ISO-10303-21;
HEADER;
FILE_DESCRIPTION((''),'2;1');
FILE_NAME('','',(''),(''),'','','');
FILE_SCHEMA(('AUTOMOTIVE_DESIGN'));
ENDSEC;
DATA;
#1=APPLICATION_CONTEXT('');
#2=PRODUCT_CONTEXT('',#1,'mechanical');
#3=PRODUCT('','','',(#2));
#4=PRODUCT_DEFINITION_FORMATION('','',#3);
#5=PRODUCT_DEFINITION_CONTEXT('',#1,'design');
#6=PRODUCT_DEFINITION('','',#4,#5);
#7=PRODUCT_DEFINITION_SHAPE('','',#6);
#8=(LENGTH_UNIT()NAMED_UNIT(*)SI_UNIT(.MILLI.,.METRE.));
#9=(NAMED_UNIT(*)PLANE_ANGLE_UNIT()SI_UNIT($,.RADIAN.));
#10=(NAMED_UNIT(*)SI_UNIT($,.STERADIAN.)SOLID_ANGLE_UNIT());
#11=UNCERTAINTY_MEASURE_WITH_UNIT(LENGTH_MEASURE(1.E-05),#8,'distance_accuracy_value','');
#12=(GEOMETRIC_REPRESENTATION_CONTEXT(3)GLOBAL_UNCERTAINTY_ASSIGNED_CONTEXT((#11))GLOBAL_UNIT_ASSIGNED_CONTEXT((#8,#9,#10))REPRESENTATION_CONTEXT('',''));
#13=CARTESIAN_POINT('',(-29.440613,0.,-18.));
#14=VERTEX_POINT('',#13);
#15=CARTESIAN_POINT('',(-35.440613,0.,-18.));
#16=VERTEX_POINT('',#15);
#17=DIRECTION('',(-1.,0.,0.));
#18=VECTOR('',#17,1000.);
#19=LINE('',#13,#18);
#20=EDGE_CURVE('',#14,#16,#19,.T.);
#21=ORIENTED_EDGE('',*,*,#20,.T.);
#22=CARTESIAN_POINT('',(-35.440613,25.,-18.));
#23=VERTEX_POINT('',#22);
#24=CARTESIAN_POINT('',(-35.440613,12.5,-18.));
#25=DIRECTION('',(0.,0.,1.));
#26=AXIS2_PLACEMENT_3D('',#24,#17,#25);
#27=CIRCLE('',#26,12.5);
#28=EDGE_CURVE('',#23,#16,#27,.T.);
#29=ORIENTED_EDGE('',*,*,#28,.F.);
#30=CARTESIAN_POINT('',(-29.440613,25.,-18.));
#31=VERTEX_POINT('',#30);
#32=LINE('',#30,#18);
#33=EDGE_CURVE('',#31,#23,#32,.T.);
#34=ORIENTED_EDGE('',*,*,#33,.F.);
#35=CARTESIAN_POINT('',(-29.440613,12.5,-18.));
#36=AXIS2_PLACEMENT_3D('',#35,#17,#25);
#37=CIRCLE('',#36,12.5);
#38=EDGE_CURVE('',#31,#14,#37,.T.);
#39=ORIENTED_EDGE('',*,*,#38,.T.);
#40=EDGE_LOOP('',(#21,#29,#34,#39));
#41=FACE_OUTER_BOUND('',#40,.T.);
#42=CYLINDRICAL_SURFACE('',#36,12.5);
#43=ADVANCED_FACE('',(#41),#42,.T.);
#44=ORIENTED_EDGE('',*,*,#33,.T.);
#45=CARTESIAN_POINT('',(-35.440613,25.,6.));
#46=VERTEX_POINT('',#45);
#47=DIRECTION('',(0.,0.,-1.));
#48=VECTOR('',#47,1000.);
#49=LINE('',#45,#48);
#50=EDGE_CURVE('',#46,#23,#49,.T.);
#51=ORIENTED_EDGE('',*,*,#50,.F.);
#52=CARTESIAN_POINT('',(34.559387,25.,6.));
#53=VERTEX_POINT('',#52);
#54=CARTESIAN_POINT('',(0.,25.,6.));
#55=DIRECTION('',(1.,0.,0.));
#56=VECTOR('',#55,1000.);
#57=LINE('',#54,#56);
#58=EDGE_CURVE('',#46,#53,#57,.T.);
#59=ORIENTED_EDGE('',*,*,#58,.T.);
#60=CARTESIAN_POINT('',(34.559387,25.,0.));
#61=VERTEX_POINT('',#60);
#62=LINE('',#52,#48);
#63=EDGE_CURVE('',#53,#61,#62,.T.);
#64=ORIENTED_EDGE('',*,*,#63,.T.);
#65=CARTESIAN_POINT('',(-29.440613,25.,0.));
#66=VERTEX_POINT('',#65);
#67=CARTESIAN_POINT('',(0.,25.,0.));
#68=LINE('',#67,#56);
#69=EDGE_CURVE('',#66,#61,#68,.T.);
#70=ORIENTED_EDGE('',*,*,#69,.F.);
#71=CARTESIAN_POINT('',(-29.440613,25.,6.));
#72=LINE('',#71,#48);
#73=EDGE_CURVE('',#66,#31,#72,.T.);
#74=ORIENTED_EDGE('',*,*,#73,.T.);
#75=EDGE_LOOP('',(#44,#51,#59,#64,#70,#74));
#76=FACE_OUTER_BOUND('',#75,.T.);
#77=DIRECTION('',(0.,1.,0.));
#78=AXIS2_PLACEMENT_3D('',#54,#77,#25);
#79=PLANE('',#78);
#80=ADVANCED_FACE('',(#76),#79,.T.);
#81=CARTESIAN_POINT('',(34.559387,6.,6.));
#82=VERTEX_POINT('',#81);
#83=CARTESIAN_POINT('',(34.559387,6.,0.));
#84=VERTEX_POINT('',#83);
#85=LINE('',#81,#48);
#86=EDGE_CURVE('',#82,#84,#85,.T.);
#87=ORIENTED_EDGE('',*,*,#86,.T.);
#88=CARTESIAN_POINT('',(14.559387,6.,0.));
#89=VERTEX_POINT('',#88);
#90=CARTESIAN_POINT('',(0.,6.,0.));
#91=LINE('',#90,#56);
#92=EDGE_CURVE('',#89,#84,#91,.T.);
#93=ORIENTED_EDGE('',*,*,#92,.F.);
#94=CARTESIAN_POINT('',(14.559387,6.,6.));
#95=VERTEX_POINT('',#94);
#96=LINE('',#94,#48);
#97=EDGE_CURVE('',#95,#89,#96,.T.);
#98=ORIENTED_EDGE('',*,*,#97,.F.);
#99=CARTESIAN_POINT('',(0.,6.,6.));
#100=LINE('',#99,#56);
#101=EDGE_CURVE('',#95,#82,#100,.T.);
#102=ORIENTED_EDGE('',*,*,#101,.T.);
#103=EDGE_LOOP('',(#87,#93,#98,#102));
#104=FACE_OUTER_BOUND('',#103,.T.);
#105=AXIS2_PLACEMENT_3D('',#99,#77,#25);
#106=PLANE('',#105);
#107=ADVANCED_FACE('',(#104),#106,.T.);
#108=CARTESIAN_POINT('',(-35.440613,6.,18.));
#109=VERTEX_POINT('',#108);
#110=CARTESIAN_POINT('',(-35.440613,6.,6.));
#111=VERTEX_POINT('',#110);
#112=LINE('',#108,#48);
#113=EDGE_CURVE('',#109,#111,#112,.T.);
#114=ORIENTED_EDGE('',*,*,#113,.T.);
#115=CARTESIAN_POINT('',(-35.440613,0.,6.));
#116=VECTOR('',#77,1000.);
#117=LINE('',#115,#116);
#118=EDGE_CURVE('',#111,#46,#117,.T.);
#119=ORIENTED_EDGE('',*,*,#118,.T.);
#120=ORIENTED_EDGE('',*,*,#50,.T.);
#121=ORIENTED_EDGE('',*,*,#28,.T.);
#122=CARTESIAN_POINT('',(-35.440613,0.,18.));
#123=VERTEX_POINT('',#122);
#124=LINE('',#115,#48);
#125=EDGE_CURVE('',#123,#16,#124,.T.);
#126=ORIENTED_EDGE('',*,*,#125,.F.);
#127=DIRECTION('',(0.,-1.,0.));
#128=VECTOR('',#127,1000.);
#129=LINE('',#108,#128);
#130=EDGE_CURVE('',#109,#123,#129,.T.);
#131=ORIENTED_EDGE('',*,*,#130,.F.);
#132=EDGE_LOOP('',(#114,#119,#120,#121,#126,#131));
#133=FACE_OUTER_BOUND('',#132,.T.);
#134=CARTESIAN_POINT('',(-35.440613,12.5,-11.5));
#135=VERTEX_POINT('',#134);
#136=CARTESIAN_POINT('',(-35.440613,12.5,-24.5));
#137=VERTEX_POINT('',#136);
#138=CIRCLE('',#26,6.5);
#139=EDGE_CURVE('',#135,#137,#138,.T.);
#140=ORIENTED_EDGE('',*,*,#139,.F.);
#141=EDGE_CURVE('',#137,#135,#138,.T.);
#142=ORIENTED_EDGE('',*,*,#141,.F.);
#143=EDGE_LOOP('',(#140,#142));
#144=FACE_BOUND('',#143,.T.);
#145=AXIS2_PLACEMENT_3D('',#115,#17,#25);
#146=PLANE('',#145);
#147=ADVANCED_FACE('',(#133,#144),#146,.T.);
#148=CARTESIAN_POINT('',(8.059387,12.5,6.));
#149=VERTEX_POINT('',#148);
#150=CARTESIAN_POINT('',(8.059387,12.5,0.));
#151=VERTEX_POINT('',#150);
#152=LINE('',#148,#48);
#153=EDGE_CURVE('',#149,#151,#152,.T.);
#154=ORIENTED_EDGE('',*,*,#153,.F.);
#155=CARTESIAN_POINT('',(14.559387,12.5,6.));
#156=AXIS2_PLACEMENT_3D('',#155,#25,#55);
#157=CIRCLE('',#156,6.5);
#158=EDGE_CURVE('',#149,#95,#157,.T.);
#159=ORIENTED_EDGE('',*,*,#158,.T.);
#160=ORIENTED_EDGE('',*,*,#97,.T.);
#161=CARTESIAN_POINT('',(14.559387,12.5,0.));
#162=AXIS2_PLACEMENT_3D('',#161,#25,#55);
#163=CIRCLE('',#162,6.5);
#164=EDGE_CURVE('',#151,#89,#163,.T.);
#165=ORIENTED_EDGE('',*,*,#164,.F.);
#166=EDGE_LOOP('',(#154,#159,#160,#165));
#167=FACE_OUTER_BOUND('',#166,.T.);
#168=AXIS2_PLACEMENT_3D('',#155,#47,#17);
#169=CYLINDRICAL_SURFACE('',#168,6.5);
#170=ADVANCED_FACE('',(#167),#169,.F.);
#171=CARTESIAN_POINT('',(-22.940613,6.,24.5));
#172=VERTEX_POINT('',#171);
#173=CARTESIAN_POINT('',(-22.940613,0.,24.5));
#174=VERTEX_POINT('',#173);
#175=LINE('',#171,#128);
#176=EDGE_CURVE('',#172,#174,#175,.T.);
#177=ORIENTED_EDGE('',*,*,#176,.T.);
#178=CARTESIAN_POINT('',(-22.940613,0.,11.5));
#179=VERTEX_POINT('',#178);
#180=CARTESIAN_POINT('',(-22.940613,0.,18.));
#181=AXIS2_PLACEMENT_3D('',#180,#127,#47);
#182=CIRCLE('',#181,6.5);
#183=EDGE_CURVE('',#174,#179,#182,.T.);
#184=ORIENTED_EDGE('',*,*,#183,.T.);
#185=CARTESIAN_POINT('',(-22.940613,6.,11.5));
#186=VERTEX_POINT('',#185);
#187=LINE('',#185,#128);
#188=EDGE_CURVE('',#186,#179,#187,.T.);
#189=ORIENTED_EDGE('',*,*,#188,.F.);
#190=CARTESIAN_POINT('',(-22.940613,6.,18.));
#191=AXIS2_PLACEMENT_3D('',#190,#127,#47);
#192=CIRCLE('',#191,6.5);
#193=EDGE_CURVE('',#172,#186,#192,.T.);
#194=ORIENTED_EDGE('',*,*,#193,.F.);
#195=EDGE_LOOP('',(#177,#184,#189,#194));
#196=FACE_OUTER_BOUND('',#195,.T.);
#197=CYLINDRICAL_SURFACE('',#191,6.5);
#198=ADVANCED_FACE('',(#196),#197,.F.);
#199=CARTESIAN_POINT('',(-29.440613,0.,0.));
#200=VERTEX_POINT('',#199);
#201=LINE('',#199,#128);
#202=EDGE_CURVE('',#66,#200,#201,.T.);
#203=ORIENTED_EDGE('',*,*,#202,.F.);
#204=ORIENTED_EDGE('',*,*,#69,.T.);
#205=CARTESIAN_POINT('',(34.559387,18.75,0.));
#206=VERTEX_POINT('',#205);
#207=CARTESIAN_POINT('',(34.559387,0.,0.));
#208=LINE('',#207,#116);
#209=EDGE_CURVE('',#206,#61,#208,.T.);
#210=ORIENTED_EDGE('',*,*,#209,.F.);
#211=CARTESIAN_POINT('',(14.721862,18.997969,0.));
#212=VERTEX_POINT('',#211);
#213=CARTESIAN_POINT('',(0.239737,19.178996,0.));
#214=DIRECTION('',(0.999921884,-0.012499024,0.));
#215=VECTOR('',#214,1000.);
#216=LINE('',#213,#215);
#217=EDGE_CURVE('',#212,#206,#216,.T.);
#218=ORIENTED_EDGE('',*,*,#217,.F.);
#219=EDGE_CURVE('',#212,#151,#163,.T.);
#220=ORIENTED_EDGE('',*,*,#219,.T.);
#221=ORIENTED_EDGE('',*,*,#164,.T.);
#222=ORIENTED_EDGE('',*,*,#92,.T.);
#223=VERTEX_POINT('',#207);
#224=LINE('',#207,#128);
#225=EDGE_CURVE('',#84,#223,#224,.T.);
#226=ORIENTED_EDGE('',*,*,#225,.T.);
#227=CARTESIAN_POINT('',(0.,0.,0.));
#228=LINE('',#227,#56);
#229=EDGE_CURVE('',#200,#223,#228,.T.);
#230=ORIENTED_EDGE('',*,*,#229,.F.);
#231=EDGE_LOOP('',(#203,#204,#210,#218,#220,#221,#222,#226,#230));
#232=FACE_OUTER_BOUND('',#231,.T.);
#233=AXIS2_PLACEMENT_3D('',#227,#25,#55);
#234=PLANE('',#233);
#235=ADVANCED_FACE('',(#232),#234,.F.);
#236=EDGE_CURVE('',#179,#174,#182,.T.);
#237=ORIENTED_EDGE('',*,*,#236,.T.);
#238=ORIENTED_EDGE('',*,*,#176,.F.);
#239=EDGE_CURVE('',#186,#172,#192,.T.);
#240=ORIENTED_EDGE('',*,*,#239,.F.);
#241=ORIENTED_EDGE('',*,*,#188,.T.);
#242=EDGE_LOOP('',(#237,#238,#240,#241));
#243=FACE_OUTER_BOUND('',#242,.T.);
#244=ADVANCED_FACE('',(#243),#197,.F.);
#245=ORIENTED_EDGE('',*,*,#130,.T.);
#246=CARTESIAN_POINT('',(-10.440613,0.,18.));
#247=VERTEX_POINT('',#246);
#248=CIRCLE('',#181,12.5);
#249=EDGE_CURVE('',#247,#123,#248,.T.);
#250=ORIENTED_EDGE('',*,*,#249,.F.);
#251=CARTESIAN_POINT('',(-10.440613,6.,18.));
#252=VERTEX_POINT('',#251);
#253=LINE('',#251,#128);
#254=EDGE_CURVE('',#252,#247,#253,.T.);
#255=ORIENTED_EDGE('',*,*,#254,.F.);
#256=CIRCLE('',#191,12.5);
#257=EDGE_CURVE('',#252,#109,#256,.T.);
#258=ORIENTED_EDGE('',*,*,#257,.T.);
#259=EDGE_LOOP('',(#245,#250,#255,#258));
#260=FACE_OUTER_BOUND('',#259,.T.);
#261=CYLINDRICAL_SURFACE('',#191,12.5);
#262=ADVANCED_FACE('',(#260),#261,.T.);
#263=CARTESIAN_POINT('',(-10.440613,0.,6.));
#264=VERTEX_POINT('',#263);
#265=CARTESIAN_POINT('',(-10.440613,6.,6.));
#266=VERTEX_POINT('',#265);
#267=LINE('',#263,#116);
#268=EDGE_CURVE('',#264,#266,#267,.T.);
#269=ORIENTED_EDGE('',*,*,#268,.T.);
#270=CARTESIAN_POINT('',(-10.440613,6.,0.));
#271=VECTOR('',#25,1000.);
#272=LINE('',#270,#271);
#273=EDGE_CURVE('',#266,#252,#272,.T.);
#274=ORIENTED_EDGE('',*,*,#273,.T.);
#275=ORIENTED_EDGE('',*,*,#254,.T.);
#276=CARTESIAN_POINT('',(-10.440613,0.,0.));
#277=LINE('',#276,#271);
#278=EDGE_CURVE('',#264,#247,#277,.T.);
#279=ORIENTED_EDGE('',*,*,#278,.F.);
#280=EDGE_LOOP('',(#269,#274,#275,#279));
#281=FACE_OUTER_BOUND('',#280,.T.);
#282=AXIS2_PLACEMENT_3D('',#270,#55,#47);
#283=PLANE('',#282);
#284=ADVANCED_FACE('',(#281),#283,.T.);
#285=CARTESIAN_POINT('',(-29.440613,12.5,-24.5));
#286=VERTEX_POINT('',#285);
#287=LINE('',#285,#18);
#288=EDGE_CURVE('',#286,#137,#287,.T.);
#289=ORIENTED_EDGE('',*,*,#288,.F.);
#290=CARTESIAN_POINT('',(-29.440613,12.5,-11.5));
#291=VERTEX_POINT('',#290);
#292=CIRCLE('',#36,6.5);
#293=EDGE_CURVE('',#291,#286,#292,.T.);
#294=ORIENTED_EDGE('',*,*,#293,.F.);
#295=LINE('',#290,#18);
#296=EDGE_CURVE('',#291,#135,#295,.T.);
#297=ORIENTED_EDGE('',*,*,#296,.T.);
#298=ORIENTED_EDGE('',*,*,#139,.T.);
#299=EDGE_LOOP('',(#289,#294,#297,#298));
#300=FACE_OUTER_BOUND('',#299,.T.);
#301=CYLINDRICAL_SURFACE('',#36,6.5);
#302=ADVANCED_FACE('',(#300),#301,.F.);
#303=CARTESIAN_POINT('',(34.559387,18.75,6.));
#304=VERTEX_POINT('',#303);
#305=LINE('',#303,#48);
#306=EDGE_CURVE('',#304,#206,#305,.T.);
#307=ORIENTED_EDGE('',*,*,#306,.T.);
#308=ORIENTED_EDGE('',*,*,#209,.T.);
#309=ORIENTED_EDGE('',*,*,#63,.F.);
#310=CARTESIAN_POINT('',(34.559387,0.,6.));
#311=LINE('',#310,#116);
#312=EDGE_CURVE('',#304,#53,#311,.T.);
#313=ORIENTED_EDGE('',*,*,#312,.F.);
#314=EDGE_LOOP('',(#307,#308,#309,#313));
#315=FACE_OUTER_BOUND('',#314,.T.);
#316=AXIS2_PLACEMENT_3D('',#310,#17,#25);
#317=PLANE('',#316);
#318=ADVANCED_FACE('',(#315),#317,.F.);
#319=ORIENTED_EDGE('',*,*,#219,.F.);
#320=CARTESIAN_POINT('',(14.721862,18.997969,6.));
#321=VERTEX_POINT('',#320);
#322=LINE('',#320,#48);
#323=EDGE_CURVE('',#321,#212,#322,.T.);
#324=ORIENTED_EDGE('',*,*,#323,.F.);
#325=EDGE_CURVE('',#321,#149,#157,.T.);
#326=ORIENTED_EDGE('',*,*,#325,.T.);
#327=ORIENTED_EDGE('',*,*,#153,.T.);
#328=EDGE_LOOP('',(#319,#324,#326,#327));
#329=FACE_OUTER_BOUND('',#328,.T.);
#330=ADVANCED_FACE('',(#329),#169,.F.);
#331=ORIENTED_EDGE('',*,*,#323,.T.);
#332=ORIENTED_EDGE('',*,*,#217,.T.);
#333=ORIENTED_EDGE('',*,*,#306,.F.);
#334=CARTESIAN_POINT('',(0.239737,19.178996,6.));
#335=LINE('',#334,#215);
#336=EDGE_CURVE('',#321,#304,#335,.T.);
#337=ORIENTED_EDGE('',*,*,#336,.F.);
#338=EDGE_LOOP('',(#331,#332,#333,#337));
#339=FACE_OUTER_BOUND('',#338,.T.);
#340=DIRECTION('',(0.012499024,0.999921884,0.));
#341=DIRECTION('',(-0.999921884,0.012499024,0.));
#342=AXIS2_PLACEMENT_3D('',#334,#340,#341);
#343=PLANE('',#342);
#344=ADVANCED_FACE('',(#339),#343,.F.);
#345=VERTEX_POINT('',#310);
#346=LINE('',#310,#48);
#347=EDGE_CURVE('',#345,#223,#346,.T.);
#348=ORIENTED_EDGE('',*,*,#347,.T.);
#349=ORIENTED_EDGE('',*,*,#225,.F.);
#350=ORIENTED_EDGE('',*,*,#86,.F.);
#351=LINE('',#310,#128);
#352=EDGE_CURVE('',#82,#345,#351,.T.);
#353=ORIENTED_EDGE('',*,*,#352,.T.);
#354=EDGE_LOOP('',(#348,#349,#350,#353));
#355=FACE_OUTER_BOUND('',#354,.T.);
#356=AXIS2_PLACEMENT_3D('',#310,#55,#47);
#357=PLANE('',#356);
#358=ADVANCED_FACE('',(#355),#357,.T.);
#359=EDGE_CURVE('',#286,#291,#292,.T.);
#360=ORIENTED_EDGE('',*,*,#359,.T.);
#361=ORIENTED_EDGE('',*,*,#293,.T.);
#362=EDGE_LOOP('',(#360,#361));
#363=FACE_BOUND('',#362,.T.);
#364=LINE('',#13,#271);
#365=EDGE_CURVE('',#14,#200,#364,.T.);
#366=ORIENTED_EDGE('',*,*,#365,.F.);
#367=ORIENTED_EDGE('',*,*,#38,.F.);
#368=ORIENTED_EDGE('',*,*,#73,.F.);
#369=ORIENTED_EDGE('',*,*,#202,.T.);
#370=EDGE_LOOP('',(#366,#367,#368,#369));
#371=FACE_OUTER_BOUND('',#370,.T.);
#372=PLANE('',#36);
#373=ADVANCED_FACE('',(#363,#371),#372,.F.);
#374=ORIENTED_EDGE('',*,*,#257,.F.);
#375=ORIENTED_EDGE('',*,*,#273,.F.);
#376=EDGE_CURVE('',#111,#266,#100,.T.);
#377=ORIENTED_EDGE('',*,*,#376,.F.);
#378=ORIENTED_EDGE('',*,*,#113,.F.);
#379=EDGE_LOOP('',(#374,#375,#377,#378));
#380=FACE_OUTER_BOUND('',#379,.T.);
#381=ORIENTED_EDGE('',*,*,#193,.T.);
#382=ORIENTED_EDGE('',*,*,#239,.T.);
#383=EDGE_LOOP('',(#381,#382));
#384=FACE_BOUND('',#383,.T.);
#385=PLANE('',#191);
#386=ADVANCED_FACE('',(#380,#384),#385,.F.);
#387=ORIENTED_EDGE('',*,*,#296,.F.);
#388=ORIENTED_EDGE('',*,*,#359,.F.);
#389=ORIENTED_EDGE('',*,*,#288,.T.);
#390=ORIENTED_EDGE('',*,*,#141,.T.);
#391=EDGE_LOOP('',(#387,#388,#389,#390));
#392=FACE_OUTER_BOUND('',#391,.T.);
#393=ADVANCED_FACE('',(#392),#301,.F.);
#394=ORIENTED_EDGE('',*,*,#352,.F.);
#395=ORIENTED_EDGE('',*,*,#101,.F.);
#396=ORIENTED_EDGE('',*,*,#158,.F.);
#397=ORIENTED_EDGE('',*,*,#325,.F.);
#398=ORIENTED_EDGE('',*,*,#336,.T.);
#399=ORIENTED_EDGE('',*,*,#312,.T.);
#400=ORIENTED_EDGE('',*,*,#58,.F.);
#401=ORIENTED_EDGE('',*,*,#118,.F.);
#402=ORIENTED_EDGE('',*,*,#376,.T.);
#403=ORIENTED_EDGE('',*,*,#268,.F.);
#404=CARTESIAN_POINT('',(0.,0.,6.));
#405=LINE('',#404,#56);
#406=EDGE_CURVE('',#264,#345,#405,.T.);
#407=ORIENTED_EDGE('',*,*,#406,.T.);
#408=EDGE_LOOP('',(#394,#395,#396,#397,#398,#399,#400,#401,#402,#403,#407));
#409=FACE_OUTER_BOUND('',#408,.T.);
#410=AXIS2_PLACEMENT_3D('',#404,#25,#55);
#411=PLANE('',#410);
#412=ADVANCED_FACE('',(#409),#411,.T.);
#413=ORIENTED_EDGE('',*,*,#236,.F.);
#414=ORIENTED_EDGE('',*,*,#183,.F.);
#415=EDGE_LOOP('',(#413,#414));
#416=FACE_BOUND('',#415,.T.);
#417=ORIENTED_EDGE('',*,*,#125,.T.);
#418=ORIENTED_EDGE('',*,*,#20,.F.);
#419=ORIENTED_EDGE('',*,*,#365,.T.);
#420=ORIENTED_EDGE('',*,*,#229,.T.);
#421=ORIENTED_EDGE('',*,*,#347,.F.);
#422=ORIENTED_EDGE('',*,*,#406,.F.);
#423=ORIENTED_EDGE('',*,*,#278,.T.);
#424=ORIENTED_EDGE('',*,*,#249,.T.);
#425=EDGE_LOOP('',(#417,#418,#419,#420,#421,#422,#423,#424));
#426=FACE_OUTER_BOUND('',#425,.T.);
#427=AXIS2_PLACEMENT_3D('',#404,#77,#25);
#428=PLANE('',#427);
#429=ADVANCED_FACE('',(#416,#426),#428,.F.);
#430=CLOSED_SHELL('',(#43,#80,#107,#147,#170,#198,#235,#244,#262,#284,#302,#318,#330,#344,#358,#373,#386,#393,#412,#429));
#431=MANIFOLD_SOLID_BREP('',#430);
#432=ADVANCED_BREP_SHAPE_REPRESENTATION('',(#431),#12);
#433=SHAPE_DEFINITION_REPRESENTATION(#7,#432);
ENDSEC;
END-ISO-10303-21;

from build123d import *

# Parameters (mm, degrees)
SLOTTED_BRACKET_BODY_DEPTH = 6
LUG_A_SKETCH_R             = 6.5
MOUNTING_LUG_A_13_DEPTH    = 6
LUG_B_SKETCH_R             = 6.5
MOUNTING_LUG_B_13_DEPTH    = 6


with BuildPart() as part:
    # Bracket Profile Sketch → Slotted Bracket Body (new body)
    with BuildSketch(Plane.XY):
        with BuildLine():
            Line((-35.440613027, 25), (-35.440613027, 0))
            Line((-35.440613027, 0), (34.559386973, 0))
            Line((34.559386973, 0), (34.559386973, 6))
            Line((34.559386973, 6), (14.559386973, 6))
            ThreePointArc((14.559386973, 6), (8.059386973, 12.5), (14.559386973, 19))
            ThreePointArc((14.559386973, 19), (14.640630626, 18.999492247), (14.721861587, 18.997969067))
            Line((14.721861587, 18.997969067), (34.559386973, 18.75))
            Line((34.559386973, 18.75), (34.559386973, 25))
            Line((34.559386973, 25), (-35.440613027, 25))
        make_face()
    extrude(amount=SLOTTED_BRACKET_BODY_DEPTH)

    # Lug A Sketch → Mounting Lug A Ø13 (add)
    with BuildSketch(Plane.ZY.offset(35.440613027)):
        with BuildLine():
            Line((-18, 0), (6, 0))
            Line((6, 0), (6, 25))
            Line((6, 25), (-18, 25))
            ThreePointArc((-18, 25), (-30.5, 12.5), (-18, 0))
        make_face()
        with Locations((-18, 12.5)):
            Circle(LUG_A_SKETCH_R, mode=Mode.SUBTRACT)
    extrude(amount=-MOUNTING_LUG_A_13_DEPTH)

    # Lug B Sketch → Mounting Lug B Ø13 (add)
    with BuildSketch(Plane.XZ):
        with BuildLine():
            Line((-35.440613027, 18), (-35.440613027, 0))
            Line((-35.440613027, 0), (-10.440613027, 0))
            Line((-10.440613027, 0), (-10.440613027, 18))
            ThreePointArc((-10.440613027, 18), (-22.940613027, 30.5), (-35.440613027, 18))
        make_face()
        with Locations(Location((-22.940613027, 18, 0), (0, 0, 270))):
            Circle(LUG_B_SKETCH_R, mode=Mode.SUBTRACT)
    extrude(amount=-MOUNTING_LUG_B_13_DEPTH)


solid = part.part
